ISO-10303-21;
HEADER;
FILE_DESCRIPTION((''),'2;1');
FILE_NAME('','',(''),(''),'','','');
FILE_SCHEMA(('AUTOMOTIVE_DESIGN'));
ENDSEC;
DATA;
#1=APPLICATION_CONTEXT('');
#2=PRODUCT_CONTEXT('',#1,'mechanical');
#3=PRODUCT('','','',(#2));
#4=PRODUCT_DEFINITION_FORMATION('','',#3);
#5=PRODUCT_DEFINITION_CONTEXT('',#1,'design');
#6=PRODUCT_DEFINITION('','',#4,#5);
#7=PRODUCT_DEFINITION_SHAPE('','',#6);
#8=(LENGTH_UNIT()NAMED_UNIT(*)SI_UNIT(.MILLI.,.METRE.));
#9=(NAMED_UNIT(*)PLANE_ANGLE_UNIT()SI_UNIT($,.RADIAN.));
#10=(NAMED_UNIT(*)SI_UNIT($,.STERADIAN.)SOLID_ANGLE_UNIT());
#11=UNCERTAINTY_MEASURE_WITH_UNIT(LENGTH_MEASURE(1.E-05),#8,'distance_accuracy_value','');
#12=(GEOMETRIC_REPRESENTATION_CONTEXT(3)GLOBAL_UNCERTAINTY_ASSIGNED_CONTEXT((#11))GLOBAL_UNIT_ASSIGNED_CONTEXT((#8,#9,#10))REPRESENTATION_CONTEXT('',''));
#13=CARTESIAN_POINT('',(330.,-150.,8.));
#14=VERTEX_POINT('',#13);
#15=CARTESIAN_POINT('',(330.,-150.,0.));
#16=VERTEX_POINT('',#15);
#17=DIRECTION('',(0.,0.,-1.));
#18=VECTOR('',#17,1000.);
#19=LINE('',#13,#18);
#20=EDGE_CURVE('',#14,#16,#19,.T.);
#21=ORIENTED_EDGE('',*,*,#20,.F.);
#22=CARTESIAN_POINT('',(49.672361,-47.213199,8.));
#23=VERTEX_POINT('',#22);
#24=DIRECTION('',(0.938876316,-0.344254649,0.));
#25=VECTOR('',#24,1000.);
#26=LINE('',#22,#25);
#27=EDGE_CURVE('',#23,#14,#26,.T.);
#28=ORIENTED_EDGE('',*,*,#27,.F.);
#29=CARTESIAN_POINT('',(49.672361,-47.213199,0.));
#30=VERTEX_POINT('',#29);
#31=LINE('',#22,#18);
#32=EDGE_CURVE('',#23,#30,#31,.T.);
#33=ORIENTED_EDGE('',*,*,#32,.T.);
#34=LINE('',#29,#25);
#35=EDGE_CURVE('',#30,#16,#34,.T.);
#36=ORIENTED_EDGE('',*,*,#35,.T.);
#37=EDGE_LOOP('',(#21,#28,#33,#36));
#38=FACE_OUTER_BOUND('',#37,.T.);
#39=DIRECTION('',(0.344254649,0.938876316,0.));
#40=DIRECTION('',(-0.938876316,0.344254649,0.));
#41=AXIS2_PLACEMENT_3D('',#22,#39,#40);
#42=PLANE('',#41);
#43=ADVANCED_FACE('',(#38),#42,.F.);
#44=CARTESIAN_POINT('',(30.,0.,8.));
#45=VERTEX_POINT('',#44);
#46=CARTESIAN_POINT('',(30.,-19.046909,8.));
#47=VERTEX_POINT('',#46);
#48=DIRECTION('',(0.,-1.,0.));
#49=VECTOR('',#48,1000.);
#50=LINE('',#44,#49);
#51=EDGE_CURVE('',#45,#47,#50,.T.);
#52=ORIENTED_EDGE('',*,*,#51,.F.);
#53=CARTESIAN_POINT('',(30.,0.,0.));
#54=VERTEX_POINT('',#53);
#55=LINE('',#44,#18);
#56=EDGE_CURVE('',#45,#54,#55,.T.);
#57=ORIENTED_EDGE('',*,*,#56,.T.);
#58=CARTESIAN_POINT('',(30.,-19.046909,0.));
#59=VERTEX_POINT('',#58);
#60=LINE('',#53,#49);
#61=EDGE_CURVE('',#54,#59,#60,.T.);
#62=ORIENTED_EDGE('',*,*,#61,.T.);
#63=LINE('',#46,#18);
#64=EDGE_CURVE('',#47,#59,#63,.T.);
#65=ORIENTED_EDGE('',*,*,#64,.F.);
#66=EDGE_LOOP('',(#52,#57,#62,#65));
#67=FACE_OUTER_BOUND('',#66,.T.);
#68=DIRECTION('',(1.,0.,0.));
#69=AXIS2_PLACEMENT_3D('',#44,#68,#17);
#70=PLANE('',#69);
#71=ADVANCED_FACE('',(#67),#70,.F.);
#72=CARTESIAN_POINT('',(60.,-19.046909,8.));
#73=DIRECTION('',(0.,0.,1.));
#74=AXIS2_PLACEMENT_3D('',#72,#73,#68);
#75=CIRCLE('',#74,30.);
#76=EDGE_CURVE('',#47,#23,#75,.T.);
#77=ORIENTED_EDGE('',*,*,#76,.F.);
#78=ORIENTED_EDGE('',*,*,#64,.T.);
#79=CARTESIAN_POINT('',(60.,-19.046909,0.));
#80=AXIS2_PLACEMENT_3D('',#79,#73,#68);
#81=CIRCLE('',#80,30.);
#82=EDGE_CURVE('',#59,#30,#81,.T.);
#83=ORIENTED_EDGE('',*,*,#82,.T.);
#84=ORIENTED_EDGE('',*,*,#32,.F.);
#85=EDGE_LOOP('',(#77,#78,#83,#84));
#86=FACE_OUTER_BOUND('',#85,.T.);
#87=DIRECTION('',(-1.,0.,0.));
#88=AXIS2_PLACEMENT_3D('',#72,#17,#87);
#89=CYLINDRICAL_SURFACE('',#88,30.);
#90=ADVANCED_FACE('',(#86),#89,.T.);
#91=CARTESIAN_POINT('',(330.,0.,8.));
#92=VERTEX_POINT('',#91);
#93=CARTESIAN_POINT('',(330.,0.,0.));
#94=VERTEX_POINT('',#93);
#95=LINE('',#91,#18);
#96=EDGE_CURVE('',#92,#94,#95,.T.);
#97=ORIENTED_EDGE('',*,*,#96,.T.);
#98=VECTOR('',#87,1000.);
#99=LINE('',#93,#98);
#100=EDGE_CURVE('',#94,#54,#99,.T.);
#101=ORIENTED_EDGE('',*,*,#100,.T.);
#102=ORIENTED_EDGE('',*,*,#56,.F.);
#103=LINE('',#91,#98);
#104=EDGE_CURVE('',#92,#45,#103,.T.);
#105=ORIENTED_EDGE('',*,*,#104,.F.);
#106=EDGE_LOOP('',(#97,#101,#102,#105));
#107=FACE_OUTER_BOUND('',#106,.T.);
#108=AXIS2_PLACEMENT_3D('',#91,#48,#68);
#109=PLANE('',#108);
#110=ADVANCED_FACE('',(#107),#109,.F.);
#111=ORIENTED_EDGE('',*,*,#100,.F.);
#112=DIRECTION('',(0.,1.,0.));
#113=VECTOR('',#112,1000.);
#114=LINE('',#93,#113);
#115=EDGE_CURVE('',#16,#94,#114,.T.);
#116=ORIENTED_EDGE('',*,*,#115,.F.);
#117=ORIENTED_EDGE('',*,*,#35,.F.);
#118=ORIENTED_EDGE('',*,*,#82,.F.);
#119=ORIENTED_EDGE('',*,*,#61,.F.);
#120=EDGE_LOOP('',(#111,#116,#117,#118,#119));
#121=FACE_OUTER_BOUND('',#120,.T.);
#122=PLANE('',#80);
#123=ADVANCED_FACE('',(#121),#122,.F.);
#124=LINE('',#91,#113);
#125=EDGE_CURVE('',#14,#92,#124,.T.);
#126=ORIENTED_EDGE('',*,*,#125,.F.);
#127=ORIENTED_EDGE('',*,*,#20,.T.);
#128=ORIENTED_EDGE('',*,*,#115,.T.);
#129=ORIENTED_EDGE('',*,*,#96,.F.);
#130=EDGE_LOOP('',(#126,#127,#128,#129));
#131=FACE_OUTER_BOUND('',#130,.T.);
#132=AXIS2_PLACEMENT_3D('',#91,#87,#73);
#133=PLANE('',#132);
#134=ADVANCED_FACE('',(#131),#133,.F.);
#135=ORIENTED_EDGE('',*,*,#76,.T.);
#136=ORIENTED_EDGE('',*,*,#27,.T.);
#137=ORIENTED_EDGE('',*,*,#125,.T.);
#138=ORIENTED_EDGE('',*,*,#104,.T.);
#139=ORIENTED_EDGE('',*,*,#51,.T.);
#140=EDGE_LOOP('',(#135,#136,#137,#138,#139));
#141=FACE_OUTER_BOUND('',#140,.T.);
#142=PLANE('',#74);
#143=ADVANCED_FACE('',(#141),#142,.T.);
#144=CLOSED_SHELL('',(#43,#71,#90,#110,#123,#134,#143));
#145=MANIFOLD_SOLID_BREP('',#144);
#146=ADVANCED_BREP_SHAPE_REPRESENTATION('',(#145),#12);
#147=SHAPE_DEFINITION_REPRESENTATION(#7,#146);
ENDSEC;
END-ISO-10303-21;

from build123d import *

# Parameters (mm, degrees)
EXTRUDE_2_DEPTH = 8


with BuildPart() as part:
    # 草图1 → 凸台-拉伸2 (new body)
    with BuildSketch(Plane.XY):
        with BuildLine():
            Line((330, 0), (30, 0))
            Line((30, 0), (30, -19.046909383))
            ThreePointArc((30, -19.046909383), (35.404988471, -36.22495956), (49.672360525, -47.213198859))
            Line((49.672360525, -47.213198859), (330, -150))
            Line((330, -150), (330, 0))
        make_face()
    extrude(amount=EXTRUDE_2_DEPTH)


solid = part.part
